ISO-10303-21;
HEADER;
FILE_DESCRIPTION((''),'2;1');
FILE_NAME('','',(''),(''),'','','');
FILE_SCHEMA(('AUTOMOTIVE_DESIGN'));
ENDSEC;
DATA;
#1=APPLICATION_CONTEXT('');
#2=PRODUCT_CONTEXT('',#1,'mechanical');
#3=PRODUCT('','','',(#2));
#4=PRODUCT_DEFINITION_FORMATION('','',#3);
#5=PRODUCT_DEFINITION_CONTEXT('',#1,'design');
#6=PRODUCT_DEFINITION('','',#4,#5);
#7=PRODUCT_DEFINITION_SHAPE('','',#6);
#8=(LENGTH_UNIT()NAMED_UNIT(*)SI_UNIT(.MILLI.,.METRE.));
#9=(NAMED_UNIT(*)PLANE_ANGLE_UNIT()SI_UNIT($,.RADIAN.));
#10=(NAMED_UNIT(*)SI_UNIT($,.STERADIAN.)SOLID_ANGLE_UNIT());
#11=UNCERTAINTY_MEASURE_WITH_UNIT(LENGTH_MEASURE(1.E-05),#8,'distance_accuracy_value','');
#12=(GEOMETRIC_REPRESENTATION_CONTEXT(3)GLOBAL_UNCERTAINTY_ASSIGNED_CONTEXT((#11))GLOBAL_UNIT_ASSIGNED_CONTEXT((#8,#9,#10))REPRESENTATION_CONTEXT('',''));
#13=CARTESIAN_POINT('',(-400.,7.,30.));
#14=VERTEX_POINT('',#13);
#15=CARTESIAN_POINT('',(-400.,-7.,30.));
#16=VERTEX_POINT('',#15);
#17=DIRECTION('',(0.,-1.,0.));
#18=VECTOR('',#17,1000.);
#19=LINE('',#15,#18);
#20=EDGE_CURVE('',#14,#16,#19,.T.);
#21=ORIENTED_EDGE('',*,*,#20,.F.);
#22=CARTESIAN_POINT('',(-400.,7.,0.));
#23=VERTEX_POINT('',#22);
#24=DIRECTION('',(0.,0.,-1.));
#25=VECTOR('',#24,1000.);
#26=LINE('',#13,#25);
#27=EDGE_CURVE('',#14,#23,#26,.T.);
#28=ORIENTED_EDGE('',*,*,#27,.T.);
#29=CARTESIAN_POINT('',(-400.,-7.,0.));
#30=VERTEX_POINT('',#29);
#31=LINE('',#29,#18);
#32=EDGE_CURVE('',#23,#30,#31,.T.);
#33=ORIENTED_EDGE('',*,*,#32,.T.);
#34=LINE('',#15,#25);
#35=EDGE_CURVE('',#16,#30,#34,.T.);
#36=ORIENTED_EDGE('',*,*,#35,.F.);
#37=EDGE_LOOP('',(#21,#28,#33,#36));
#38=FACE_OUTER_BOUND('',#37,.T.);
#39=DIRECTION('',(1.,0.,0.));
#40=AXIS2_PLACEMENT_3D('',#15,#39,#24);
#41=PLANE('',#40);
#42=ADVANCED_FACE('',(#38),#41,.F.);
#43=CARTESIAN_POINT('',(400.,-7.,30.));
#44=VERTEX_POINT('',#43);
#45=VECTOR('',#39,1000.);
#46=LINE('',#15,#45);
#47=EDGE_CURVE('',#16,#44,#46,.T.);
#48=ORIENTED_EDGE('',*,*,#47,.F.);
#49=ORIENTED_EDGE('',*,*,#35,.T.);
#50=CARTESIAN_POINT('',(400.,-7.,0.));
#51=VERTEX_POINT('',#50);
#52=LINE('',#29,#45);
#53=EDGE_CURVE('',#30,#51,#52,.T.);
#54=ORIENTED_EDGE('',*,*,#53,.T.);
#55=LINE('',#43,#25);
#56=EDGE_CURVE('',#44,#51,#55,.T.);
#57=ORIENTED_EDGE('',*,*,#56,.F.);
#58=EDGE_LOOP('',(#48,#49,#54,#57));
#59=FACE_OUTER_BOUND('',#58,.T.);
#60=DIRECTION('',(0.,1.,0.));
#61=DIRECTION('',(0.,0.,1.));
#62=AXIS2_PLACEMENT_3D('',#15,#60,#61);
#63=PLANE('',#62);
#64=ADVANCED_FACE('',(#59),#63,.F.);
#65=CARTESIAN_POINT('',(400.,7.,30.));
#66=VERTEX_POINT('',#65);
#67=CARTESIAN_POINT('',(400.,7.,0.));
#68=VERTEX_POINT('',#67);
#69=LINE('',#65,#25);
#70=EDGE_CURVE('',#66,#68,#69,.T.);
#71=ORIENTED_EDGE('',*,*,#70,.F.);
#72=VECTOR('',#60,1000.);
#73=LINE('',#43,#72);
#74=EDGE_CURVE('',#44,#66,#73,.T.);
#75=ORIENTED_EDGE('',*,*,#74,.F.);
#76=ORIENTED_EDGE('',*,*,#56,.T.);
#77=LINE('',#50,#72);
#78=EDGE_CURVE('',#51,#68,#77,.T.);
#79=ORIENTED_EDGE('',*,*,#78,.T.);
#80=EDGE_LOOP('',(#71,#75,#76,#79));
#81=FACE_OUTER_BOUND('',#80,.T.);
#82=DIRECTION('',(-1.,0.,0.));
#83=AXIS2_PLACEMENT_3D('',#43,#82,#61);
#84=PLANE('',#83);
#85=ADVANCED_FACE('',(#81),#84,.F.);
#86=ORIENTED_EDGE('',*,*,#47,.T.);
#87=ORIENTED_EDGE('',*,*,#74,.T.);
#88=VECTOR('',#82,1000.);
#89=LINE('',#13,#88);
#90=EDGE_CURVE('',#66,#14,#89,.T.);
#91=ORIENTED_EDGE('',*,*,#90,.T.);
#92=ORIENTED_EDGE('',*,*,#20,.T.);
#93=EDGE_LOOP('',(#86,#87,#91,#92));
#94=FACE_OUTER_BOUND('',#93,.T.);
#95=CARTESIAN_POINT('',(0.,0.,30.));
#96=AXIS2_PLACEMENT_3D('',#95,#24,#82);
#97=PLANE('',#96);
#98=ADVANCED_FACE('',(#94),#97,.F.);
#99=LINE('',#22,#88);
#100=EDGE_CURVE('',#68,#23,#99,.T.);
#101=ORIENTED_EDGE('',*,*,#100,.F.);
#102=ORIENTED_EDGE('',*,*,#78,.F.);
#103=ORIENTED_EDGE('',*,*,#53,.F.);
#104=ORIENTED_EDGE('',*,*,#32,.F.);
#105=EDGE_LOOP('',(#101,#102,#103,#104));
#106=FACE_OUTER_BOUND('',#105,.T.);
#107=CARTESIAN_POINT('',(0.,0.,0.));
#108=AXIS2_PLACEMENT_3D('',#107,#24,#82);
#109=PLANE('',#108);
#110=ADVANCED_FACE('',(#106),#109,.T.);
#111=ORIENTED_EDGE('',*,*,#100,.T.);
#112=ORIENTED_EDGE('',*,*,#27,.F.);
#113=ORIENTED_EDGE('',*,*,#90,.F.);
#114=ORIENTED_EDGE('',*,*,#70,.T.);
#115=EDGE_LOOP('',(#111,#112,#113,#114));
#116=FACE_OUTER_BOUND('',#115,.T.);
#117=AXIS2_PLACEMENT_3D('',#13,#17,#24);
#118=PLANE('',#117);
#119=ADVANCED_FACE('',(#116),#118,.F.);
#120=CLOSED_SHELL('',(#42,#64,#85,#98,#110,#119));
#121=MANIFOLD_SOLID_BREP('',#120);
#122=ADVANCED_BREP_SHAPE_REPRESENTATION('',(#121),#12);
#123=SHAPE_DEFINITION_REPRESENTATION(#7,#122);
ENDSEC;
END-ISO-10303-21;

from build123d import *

# Parameters (mm, degrees)
SKETCH_1_W      = 800
SKETCH_1_H      = 14
EXTRUDE_1_DEPTH = 30


with BuildPart() as part:
    # 草图1 → 凸台-拉伸1 (new body)
    with BuildSketch(Plane.XY):
        Rectangle(SKETCH_1_W, SKETCH_1_H)
    extrude(amount=EXTRUDE_1_DEPTH)


solid = part.part
